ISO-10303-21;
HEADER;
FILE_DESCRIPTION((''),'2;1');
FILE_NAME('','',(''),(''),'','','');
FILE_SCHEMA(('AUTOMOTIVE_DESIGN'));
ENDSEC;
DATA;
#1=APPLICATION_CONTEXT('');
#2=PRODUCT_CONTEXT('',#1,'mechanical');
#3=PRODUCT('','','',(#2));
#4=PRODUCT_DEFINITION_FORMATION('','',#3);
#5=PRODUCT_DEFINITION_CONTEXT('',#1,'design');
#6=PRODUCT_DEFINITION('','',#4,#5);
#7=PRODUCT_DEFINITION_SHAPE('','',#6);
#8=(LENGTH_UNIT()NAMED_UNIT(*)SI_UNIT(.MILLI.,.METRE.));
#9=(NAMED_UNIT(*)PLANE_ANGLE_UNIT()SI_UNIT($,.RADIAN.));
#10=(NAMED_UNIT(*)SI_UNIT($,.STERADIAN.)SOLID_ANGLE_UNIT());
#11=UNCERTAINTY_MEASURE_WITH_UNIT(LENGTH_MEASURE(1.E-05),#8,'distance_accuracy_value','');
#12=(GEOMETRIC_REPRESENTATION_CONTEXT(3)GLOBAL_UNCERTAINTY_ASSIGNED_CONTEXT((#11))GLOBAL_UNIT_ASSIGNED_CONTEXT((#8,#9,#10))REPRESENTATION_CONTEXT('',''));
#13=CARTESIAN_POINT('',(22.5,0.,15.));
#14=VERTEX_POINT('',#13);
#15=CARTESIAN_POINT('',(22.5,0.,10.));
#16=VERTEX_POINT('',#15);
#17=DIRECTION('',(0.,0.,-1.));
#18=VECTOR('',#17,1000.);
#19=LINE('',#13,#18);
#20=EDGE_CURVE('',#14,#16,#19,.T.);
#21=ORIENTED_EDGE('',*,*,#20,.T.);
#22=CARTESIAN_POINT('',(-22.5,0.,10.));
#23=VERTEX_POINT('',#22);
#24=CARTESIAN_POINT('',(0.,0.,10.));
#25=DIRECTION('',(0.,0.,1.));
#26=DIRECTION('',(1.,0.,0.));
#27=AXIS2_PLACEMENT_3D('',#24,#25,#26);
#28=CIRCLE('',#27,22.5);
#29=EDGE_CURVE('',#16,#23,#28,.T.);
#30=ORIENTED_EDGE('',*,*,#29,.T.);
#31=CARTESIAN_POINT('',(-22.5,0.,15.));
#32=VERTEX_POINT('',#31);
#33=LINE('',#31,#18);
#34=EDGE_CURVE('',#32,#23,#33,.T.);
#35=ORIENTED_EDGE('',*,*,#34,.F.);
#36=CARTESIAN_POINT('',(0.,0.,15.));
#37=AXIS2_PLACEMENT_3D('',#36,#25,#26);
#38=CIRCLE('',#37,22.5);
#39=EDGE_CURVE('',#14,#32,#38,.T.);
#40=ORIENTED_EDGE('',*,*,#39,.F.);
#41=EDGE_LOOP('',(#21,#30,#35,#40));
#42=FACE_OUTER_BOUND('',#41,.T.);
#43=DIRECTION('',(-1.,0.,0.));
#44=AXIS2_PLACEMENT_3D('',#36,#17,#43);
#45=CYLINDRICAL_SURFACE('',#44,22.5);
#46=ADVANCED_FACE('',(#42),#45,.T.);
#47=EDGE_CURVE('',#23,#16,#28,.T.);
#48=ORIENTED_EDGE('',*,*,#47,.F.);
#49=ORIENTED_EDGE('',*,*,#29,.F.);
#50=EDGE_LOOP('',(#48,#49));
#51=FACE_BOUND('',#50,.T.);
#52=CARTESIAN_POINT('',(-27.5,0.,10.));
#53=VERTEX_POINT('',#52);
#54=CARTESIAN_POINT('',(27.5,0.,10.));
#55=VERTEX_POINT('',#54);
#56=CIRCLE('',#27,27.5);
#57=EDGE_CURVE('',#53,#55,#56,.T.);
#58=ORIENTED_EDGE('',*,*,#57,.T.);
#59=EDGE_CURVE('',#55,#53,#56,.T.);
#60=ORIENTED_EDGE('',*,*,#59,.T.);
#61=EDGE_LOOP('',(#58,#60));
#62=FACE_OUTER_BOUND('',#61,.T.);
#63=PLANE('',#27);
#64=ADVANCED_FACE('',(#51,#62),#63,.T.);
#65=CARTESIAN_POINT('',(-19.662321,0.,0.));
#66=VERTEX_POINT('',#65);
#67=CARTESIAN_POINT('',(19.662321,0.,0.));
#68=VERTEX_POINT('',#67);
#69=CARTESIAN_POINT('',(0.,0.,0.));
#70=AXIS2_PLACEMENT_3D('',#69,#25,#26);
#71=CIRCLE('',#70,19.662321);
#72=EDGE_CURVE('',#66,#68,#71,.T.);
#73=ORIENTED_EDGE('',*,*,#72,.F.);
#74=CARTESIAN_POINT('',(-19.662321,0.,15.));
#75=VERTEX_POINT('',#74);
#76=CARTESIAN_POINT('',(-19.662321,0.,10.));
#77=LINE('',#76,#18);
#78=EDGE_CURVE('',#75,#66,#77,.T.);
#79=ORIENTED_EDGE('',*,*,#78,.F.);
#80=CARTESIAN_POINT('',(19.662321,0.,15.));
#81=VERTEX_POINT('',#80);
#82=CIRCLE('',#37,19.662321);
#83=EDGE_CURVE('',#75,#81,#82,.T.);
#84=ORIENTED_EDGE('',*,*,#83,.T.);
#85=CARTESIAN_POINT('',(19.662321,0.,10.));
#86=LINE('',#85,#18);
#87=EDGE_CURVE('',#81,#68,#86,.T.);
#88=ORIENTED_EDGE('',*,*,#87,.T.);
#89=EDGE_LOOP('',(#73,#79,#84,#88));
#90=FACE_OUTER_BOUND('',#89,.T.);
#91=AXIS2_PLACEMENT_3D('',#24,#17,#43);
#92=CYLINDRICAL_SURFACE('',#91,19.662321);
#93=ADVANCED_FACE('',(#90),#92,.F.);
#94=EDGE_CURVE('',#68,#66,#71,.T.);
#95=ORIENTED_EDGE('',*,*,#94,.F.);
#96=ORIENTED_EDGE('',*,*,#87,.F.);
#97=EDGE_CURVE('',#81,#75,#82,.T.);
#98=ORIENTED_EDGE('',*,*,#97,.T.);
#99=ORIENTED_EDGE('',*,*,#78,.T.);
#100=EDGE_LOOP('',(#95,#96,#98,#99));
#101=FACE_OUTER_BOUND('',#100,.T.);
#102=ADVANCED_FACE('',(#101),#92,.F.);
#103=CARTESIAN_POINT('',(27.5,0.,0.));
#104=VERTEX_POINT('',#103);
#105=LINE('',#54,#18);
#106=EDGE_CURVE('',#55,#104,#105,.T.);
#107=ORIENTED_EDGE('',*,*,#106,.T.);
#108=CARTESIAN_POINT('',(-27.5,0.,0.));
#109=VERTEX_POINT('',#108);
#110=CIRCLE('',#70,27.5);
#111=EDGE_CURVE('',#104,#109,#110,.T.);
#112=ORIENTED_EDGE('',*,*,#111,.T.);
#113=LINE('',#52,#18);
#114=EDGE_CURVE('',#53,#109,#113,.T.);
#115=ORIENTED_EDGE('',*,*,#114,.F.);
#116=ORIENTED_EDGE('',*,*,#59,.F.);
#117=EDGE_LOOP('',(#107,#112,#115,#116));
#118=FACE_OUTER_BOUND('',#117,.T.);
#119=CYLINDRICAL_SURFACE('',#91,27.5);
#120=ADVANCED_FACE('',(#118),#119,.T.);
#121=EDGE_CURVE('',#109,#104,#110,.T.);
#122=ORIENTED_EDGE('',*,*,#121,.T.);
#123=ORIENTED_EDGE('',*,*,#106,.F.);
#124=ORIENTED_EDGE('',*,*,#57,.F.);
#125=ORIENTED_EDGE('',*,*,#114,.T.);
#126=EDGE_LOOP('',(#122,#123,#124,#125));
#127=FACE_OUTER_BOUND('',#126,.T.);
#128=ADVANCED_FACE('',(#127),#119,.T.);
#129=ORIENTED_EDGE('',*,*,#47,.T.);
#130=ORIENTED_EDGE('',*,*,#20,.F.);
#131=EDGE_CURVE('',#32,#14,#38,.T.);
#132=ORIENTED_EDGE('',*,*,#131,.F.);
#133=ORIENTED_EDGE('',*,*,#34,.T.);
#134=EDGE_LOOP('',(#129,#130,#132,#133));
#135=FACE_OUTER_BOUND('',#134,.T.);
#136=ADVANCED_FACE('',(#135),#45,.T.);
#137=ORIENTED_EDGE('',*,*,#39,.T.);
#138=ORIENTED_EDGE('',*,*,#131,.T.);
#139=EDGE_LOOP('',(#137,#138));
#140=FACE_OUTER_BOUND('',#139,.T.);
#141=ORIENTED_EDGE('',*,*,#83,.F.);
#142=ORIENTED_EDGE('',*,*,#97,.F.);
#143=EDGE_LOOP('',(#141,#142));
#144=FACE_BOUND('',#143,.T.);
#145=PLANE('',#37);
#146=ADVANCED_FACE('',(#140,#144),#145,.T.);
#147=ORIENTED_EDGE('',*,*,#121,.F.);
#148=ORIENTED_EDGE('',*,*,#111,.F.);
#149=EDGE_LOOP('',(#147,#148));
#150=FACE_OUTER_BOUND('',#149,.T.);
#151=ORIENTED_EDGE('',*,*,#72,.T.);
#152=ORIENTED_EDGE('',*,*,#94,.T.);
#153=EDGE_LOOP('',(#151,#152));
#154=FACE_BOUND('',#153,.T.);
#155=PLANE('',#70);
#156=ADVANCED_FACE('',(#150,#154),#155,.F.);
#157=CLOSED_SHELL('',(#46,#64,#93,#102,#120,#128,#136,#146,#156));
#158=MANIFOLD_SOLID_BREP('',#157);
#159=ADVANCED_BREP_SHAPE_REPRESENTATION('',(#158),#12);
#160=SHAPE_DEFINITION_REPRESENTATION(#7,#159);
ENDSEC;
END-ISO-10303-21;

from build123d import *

# Parameters (mm, degrees)
SKETCH1_R           = 27.5
SKETCH1_R_2         = 19.662321429
BOSS_EXTRUDE1_DEPTH = 10
SKETCH2_R           = 22.5
SKETCH2_R_2         = 19.662321429
BOSS_EXTRUDE2_DEPTH = 5


with BuildPart() as part:
    # Sketch1 → Boss-Extrude1 (new body)
    with BuildSketch(Plane.XY):
        Circle(SKETCH1_R)
        Circle(SKETCH1_R_2, mode=Mode.SUBTRACT)
    extrude(amount=BOSS_EXTRUDE1_DEPTH)

    # Sketch2 → Boss-Extrude2 (add)
    with BuildSketch(Plane.XY.offset(10)):
        Circle(SKETCH2_R)
        Circle(SKETCH2_R_2, mode=Mode.SUBTRACT)
    extrude(amount=BOSS_EXTRUDE2_DEPTH)


solid = part.part
